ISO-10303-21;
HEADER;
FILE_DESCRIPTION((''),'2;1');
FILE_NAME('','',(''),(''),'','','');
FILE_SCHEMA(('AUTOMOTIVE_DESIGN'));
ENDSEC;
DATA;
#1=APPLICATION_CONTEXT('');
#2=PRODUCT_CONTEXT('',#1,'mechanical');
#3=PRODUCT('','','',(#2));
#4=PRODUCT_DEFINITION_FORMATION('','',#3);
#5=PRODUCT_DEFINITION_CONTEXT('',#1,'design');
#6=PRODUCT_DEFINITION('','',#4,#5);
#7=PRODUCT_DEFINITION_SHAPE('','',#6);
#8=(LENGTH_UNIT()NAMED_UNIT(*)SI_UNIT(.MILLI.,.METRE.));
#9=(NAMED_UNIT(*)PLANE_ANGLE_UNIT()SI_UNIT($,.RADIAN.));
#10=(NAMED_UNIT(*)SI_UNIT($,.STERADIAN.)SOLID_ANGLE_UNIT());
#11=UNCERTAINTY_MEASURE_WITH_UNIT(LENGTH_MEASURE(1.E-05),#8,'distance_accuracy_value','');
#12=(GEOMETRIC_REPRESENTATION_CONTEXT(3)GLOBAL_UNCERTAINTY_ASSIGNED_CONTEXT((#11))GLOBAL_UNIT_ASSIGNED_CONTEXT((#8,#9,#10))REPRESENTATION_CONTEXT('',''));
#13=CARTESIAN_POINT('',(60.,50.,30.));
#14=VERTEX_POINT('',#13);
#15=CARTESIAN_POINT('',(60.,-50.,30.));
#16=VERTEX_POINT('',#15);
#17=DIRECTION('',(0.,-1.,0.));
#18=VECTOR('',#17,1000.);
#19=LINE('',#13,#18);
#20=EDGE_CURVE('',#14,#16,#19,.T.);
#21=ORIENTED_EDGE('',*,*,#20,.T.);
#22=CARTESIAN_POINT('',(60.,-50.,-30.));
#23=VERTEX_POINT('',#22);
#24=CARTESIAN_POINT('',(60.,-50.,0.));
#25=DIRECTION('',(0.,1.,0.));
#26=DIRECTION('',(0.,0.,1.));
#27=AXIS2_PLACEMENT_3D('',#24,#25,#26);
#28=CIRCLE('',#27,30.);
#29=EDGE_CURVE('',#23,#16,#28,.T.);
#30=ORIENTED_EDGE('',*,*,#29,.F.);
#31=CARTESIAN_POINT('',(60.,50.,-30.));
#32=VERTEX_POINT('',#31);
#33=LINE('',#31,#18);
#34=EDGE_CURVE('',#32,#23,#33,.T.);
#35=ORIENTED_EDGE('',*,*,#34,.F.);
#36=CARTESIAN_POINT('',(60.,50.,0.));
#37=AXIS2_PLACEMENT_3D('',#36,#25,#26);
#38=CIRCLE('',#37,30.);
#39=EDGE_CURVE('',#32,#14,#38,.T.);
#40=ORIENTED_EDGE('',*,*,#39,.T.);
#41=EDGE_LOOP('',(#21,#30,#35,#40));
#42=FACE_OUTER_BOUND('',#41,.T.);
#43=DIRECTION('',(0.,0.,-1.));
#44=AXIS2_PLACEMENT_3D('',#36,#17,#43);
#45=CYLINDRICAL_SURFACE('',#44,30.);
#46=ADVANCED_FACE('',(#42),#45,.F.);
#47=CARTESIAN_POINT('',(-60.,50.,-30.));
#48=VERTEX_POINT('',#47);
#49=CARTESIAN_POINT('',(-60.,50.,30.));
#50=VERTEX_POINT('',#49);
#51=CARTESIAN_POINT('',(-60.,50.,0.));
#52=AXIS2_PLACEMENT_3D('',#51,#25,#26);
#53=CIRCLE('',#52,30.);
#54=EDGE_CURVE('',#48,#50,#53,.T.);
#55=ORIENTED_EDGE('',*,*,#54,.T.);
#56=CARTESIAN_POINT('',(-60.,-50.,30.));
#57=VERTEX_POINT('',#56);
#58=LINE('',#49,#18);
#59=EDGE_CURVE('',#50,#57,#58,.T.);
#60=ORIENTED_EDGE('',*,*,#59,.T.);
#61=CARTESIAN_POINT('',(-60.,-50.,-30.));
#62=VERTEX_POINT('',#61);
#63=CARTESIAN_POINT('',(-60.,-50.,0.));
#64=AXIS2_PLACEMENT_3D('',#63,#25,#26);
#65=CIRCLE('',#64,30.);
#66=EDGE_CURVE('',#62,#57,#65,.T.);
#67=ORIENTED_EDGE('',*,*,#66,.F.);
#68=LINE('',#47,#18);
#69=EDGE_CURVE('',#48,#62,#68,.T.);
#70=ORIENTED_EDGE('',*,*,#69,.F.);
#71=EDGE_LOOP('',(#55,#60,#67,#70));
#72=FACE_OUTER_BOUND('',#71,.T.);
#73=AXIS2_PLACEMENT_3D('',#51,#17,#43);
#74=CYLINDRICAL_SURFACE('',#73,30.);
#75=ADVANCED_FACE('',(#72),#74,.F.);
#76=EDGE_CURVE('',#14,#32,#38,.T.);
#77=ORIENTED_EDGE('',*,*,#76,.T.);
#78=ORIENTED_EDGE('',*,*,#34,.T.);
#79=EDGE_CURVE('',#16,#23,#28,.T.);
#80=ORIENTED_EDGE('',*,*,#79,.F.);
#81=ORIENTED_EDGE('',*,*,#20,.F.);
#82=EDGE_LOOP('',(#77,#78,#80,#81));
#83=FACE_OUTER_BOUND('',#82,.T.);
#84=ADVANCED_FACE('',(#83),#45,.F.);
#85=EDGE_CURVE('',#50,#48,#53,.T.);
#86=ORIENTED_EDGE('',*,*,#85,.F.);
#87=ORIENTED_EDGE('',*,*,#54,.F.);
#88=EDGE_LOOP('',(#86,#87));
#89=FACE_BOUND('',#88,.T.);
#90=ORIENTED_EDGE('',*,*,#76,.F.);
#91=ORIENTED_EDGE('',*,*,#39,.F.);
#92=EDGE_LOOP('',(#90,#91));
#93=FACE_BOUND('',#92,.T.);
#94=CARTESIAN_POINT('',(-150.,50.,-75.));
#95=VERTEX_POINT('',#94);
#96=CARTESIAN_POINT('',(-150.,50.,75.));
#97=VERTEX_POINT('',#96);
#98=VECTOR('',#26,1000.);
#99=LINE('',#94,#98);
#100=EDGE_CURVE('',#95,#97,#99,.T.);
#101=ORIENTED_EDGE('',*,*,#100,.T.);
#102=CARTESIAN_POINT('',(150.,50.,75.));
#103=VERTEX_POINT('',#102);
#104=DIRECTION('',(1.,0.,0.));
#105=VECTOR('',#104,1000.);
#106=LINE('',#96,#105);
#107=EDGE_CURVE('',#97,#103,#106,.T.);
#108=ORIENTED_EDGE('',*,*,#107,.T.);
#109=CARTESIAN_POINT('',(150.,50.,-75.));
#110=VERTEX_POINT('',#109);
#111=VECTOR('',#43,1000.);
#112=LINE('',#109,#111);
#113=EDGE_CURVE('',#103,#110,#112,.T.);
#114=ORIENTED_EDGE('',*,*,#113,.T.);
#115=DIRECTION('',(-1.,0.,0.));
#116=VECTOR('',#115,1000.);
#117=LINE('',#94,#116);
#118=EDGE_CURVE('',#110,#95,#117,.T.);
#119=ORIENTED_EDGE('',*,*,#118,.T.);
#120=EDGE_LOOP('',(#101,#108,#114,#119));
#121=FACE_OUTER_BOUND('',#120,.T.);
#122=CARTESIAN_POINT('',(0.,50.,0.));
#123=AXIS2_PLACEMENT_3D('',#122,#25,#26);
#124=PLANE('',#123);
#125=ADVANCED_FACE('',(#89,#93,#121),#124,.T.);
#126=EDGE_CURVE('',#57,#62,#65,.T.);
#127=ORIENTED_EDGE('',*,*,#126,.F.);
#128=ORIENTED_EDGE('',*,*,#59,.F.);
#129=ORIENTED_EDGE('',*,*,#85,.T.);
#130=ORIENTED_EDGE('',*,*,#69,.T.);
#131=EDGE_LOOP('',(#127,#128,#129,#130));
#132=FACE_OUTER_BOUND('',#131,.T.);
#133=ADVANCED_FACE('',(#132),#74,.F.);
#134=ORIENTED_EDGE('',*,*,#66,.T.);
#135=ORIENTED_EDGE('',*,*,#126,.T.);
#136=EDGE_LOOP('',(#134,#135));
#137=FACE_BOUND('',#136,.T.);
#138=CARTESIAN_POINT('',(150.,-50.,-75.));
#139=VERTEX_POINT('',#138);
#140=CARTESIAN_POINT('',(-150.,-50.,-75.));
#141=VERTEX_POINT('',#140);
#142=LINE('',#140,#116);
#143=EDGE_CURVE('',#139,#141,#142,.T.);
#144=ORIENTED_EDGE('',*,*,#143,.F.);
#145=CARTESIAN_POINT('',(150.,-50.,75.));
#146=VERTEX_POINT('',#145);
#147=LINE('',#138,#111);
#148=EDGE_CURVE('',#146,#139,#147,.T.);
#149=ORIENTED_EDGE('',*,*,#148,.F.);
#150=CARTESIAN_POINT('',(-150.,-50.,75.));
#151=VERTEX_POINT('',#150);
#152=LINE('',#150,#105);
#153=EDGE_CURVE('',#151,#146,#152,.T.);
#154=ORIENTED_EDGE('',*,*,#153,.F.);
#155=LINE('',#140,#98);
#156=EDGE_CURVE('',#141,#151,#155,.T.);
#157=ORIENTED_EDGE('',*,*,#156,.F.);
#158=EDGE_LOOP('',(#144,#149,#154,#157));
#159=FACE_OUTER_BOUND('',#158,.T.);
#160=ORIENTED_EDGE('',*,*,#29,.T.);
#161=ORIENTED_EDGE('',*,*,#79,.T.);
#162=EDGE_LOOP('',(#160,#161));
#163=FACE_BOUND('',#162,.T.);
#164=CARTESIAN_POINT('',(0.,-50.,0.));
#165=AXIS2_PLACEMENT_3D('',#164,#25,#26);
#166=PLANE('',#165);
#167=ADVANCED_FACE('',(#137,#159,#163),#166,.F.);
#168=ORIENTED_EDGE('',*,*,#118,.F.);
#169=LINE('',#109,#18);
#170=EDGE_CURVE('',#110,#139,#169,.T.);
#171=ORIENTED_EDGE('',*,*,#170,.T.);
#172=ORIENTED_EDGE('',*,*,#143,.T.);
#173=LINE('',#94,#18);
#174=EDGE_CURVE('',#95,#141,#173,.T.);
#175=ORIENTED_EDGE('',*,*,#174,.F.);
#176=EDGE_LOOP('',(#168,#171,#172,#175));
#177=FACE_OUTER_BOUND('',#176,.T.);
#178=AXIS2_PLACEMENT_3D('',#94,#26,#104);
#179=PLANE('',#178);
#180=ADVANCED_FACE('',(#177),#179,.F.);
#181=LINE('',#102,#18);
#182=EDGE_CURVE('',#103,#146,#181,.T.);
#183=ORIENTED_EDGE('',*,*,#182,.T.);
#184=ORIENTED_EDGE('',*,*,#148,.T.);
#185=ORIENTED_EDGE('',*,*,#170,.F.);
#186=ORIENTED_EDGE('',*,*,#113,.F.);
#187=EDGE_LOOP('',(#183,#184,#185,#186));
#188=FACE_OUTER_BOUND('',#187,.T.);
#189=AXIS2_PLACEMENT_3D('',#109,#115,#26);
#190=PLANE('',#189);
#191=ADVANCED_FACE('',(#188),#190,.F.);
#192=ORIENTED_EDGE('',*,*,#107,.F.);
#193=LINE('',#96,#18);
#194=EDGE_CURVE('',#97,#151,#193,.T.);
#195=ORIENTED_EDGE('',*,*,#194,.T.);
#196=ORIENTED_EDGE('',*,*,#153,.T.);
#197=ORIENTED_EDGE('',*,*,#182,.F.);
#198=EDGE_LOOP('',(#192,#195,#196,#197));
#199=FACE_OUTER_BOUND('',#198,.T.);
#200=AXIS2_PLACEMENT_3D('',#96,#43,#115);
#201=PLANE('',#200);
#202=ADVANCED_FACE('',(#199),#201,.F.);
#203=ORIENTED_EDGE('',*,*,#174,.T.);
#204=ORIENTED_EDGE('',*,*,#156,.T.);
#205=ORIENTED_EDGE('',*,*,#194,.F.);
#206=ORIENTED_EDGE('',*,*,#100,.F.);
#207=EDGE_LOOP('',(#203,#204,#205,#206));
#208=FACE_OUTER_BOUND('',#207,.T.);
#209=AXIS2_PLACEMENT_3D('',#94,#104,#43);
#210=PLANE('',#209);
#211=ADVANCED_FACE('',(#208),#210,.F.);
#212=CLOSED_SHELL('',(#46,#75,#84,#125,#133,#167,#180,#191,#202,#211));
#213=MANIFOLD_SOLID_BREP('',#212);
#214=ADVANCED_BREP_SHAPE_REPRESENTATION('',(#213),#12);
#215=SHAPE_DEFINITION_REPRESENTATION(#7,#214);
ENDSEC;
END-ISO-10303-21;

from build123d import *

# Parameters (mm, degrees)
SKETCH1_W           = 300
SKETCH1_H           = 150
SKETCH1_R           = 30
BOSS_EXTRUDE1_DEPTH = 50


with BuildPart() as part:
    # Sketch1 → Boss-Extrude1 (new, symmetric)
    with BuildSketch(Plane(origin=(0, 0, 0), x_dir=(1, 0, 0), z_dir=(0, 1, 0))):
        Rectangle(SKETCH1_W, SKETCH1_H)
        with Locations(Location((60, 0, 0), (0, 0, 90))):
            Circle(SKETCH1_R, mode=Mode.SUBTRACT)
        with Locations(Location((-60, 0, 0), (0, 0, 90))):
            Circle(SKETCH1_R, mode=Mode.SUBTRACT)
    extrude(amount=BOSS_EXTRUDE1_DEPTH, both=True)


solid = part.part
